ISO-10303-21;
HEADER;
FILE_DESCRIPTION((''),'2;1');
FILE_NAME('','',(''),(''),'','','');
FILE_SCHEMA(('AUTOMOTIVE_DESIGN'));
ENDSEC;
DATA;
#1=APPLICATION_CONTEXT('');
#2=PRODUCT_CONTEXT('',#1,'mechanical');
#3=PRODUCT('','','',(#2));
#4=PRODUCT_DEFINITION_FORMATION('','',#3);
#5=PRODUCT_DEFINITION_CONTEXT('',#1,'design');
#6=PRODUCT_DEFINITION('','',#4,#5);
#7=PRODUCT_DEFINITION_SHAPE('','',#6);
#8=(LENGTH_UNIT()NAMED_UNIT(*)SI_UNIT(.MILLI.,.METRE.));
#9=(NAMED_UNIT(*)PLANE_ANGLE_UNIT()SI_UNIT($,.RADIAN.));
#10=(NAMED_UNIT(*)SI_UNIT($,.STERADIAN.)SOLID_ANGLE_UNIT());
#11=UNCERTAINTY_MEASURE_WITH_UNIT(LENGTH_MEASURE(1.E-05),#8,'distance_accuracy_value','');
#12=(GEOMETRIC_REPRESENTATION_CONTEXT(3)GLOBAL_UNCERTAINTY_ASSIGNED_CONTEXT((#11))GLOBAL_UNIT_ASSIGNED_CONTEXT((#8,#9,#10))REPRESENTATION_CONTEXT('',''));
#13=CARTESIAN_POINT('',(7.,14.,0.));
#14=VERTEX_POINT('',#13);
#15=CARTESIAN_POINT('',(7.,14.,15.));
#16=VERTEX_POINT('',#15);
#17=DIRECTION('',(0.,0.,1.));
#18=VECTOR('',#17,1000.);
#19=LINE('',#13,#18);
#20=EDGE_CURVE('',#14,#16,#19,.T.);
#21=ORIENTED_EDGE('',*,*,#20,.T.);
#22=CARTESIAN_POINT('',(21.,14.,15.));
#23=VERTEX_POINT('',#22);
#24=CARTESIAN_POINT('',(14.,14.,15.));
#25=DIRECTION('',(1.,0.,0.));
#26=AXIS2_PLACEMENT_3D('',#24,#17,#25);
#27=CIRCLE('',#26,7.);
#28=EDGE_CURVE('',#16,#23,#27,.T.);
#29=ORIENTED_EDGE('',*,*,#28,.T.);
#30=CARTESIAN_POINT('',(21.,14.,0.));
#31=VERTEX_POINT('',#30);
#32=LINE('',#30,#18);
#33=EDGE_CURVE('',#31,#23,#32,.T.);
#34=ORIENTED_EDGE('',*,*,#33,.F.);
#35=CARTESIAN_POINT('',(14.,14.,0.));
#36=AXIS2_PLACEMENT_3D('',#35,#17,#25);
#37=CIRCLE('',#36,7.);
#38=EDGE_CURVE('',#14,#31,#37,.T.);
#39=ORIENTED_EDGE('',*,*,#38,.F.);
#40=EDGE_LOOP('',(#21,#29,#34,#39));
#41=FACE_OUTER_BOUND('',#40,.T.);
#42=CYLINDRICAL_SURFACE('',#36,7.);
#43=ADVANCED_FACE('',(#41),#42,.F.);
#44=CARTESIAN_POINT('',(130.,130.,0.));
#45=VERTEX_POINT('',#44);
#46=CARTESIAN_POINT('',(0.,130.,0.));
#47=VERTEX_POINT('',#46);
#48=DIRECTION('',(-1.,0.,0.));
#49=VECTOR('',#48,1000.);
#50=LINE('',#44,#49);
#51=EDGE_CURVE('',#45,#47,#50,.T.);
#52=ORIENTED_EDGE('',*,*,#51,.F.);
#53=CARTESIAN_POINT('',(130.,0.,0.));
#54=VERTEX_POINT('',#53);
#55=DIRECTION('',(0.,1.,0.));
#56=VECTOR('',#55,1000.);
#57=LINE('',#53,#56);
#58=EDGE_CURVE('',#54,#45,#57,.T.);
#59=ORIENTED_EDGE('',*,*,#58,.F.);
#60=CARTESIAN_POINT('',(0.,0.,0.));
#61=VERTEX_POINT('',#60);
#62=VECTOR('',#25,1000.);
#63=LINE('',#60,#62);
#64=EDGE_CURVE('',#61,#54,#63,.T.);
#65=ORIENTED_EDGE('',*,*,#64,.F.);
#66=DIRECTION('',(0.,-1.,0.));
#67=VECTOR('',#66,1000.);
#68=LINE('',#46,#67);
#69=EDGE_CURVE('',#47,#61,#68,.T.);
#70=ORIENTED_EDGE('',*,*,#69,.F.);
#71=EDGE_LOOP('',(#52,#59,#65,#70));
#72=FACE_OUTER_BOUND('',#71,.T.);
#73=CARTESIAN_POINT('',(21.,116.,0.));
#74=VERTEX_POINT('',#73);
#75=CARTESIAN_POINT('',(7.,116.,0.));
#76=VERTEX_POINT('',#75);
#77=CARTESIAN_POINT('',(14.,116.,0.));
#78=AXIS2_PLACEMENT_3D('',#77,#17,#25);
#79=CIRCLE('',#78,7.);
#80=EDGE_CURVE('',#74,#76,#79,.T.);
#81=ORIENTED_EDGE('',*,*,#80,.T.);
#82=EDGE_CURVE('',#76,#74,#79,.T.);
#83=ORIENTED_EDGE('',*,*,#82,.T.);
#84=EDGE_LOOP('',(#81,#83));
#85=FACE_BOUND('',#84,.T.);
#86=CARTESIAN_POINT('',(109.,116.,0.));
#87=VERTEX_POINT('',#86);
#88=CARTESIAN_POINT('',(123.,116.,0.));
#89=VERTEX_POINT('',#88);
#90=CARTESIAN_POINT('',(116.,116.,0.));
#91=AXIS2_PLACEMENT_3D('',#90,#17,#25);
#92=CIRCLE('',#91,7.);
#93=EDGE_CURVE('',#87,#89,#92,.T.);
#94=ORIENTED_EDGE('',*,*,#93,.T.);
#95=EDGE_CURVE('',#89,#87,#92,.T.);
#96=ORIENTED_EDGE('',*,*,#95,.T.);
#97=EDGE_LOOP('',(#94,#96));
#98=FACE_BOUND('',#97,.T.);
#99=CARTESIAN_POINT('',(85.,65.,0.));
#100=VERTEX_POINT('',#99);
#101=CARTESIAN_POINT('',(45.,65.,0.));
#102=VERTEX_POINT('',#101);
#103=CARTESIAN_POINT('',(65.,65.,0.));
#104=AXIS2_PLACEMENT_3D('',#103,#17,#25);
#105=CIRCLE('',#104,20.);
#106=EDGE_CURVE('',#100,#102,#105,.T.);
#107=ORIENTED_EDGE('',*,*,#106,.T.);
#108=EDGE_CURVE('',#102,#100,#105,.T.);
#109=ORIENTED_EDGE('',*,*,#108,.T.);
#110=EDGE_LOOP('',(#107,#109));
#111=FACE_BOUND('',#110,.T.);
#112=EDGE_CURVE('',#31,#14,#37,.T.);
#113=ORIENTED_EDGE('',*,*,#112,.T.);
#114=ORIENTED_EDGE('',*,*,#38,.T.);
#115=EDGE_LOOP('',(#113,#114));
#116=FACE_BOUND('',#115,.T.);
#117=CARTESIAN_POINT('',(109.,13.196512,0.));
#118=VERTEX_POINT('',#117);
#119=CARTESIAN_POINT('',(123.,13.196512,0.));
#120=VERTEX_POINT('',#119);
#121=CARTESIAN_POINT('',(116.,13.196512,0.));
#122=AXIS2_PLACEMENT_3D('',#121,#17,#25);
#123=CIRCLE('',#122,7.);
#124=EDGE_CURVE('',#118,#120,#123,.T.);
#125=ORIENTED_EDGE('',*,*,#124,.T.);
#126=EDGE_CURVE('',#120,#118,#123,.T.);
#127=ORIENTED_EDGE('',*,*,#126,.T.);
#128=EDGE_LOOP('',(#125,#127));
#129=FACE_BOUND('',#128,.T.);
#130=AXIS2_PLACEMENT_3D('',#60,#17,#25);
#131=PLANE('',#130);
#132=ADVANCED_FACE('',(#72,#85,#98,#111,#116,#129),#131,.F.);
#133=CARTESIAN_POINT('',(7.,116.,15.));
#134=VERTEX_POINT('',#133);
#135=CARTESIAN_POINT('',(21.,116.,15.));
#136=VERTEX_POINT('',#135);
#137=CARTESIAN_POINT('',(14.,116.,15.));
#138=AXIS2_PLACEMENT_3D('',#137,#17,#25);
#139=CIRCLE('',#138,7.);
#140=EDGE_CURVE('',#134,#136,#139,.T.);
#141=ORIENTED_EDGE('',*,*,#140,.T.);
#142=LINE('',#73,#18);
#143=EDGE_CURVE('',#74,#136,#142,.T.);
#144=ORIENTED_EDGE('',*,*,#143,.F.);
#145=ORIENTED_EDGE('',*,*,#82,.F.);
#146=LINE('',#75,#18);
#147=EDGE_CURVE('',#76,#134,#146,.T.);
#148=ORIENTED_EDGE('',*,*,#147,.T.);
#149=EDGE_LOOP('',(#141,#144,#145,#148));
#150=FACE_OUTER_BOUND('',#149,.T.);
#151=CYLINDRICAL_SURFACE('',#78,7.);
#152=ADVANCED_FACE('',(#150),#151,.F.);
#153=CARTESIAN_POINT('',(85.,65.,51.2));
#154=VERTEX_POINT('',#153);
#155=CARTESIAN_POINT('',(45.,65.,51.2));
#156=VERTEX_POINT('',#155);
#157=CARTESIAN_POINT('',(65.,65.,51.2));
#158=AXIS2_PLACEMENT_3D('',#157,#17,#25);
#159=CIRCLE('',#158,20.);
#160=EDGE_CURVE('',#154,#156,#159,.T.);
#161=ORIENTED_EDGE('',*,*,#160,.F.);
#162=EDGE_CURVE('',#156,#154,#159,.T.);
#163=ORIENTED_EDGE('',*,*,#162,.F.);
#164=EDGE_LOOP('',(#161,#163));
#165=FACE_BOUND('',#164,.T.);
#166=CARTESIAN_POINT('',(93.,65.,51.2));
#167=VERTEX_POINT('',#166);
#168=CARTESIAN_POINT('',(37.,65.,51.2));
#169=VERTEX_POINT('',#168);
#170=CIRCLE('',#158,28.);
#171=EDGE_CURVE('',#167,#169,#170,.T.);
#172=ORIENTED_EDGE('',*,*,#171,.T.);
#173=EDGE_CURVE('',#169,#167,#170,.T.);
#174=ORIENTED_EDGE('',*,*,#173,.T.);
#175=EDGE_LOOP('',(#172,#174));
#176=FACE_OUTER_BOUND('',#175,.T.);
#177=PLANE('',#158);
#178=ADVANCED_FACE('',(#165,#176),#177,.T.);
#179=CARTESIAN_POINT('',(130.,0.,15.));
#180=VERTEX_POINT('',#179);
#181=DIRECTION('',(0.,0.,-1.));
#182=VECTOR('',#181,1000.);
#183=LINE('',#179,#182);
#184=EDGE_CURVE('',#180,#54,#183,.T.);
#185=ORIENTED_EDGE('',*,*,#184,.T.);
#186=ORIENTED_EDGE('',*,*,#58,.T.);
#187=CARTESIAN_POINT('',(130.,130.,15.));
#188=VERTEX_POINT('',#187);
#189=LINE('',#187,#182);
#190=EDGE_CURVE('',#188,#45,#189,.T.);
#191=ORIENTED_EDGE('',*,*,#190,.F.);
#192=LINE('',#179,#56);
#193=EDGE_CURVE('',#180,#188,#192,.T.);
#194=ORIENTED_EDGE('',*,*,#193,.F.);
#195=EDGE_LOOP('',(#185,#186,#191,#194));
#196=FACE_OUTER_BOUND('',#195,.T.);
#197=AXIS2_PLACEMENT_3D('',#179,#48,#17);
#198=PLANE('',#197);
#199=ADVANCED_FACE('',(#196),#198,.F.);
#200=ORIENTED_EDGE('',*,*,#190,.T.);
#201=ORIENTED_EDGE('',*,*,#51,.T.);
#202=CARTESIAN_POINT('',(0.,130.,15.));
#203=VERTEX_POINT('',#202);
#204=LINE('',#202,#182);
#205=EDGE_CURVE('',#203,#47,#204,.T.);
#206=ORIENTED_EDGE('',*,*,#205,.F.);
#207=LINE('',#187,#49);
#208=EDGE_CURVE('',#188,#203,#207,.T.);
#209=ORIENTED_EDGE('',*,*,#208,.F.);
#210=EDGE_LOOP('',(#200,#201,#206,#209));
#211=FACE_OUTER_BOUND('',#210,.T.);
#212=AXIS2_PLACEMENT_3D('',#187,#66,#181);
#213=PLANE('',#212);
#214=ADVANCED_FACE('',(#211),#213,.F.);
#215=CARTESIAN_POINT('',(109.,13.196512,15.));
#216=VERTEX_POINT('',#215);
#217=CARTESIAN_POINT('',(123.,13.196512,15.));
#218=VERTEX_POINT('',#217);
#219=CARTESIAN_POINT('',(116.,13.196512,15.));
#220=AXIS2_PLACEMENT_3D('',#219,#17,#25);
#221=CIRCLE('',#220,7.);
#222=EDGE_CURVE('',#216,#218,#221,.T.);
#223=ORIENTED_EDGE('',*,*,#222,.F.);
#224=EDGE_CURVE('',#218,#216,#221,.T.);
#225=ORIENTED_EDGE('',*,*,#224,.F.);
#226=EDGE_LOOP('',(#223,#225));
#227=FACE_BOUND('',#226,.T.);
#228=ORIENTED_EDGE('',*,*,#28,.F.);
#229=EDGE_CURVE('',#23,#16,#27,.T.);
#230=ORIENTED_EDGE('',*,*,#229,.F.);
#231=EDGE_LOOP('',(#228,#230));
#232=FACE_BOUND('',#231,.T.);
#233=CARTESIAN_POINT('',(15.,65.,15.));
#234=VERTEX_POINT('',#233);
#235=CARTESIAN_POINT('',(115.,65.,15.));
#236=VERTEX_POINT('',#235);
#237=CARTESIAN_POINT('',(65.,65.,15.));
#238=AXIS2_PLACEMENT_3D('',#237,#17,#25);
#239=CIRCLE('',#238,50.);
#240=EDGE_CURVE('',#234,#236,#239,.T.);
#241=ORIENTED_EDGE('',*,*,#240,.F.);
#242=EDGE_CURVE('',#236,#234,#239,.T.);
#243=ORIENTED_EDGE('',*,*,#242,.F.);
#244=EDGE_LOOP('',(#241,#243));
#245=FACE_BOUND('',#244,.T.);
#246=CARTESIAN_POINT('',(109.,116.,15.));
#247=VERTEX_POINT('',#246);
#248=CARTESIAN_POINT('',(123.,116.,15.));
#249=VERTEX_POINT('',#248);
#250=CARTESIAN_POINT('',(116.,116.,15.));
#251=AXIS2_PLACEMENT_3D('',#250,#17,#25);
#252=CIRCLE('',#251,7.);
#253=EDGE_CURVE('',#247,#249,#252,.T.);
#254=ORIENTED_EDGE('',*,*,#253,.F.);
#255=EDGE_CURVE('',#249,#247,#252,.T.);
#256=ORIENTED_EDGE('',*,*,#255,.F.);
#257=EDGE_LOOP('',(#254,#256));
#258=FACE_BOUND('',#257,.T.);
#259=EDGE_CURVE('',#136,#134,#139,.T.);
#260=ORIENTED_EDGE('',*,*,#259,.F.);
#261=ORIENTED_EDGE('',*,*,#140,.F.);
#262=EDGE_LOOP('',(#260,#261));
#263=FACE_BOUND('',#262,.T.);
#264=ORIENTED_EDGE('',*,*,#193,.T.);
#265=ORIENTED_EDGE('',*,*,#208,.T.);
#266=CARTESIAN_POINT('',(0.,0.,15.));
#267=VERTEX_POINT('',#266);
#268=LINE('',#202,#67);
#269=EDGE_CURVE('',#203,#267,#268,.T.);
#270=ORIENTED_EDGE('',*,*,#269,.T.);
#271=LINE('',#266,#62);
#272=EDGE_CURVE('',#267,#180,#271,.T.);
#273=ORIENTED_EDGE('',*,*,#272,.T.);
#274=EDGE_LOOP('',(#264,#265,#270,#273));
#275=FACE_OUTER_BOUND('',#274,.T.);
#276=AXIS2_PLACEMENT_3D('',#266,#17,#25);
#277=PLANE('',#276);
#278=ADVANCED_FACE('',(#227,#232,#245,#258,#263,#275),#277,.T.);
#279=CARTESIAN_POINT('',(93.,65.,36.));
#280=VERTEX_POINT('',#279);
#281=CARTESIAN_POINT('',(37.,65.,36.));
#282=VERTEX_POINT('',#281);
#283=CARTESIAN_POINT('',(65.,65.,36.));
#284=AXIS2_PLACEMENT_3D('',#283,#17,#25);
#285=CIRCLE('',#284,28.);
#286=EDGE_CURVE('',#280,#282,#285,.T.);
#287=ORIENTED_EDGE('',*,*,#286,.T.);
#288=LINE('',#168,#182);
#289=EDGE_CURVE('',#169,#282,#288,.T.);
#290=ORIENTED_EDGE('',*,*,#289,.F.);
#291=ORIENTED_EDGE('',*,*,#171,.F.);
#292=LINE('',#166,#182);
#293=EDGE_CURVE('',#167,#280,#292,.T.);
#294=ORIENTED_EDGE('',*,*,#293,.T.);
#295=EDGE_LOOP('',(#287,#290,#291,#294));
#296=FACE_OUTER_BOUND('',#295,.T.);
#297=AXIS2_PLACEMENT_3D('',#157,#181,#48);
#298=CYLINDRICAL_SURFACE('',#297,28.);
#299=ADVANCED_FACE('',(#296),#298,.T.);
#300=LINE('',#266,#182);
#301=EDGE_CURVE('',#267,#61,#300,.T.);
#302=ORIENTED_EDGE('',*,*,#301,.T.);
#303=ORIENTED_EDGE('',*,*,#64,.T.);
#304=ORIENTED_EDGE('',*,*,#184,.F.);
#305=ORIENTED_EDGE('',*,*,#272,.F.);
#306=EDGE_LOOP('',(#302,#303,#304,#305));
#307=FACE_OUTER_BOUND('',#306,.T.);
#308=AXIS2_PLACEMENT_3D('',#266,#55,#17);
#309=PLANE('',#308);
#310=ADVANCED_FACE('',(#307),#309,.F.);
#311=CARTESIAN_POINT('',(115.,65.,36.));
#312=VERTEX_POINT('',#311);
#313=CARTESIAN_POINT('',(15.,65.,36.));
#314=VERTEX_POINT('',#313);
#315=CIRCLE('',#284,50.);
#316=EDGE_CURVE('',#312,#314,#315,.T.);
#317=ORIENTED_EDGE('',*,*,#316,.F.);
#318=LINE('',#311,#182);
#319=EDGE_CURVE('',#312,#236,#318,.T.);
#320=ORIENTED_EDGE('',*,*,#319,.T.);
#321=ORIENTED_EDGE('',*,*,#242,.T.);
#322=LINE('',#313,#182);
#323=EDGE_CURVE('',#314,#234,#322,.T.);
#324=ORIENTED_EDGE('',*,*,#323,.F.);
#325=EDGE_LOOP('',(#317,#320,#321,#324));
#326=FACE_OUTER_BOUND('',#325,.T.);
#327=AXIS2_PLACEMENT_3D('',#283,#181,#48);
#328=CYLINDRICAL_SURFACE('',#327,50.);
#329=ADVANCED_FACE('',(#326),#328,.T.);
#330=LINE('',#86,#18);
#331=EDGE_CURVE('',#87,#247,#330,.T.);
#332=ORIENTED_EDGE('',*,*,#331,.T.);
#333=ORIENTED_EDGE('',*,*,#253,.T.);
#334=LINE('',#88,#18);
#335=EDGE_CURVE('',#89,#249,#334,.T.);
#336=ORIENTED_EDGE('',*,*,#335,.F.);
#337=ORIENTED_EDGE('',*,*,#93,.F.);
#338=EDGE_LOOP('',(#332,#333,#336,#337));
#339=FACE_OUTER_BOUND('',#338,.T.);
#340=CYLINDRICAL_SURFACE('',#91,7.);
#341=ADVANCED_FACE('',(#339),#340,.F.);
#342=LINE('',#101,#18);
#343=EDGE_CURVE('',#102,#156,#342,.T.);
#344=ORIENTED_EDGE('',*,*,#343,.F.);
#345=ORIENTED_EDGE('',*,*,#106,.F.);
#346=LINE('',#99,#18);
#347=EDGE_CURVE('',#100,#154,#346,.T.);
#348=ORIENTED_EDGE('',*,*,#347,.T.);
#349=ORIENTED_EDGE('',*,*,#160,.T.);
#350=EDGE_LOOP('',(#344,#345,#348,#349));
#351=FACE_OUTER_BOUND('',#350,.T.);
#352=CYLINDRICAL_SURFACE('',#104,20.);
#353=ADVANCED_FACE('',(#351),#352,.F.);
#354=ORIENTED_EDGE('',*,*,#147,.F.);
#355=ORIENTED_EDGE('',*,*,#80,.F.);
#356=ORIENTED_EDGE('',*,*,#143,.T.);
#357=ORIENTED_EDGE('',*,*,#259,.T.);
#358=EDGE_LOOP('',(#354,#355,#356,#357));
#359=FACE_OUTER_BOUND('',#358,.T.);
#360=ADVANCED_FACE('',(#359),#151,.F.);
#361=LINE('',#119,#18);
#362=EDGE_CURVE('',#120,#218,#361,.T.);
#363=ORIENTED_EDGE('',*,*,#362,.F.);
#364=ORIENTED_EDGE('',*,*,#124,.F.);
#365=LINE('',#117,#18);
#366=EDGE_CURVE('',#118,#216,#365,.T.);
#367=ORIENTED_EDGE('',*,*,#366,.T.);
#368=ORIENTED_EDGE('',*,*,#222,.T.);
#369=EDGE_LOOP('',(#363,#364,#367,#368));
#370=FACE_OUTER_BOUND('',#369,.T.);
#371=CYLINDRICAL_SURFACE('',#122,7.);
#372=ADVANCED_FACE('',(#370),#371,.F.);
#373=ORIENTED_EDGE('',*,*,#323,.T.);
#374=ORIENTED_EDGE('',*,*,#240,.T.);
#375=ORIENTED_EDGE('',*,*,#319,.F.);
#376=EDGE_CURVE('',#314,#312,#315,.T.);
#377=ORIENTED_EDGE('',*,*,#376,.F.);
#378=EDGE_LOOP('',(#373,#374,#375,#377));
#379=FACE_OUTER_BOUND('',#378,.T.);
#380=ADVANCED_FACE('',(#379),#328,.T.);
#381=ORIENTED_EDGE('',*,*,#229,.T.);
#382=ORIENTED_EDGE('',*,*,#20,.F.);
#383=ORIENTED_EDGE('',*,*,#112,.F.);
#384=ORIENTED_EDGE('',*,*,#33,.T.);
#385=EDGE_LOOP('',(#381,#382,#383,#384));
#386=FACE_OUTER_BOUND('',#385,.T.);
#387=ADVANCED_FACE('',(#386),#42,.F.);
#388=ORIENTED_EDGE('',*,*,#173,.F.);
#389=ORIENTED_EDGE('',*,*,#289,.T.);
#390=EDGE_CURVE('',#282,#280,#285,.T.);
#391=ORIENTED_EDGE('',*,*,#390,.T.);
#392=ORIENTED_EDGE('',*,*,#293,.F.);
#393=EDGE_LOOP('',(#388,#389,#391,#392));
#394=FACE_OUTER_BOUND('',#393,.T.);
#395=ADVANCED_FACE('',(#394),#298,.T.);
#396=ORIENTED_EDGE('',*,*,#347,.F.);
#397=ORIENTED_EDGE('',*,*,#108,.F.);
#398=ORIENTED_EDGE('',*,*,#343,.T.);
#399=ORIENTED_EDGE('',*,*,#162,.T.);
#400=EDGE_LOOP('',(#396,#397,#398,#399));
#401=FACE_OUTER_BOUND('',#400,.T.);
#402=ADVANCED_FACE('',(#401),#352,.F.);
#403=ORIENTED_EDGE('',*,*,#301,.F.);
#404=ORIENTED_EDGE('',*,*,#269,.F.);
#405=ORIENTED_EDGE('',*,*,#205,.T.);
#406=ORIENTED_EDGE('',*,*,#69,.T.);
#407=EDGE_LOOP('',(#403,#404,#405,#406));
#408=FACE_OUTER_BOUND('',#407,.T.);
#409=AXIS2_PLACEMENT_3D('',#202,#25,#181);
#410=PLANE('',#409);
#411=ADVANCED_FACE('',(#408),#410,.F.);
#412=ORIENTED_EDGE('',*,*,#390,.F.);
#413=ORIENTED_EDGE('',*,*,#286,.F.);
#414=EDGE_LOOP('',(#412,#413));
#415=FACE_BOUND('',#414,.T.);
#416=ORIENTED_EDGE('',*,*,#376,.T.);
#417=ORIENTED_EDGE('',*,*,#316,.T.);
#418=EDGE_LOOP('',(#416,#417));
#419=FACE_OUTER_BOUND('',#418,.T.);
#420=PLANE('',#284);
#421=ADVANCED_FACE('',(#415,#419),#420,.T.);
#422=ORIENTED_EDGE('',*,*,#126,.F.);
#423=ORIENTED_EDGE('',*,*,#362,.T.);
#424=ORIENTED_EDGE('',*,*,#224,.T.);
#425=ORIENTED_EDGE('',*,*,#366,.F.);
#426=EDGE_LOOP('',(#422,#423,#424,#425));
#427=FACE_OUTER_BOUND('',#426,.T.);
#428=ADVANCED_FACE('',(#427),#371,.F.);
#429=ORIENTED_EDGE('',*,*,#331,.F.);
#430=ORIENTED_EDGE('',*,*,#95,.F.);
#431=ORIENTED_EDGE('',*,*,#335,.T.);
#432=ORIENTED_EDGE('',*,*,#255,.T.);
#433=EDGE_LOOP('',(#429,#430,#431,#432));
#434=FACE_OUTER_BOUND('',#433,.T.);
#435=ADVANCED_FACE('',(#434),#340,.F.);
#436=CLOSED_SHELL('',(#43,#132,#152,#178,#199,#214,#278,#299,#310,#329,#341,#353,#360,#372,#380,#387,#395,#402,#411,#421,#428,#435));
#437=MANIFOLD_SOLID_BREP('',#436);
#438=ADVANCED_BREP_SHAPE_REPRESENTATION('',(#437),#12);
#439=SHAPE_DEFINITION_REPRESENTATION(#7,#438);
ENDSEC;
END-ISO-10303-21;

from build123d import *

# Parameters (mm, degrees)
FLANGE_PLATE_SKETCH_W         = 130
FLANGE_PLATE_SKETCH_H         = 130
FLANGE_PLATE_130X130X15_DEPTH = 15
HUB_SKETCH_100_R              = 50
HUB_100_DEPTH                 = 21
SPIGOT_SKETCH_56_R            = 28
SPIGOT_56_DEPTH               = 15.2
BORE_SKETCH_40_R              = 20
BORE_40_DEPTH                 = 51.2
MOUNTING_HOLES_SKETCH_R       = 7
MOUNTING_HOLES_4X_14_DEPTH    = 15


with BuildPart() as part:
    # Flange Plate Sketch → Flange Plate 130x130x15 (new body)
    with BuildSketch(Plane.XY):
        with Locations((65, 65)):
            Rectangle(FLANGE_PLATE_SKETCH_W, FLANGE_PLATE_SKETCH_H)
    extrude(amount=FLANGE_PLATE_130X130X15_DEPTH)

    # Hub Sketch Ø100 → Hub Ø100 (add)
    with BuildSketch(Plane.XY.offset(15)):
        with Locations(Location((65, 65, 0), (0, 0, 180))):
            Circle(HUB_SKETCH_100_R)
    extrude(amount=HUB_100_DEPTH)

    # Spigot Sketch Ø56 → Spigot Ø56 (add)
    with BuildSketch(Plane.XY.offset(36)):
        with Locations(Location((65, 65, 0), (0, 0, 180))):
            Circle(SPIGOT_SKETCH_56_R)
    extrude(amount=SPIGOT_56_DEPTH)

    # Bore Sketch Ø40 → Bore Ø40 (cut)
    with BuildSketch(Plane.XY.offset(51.2)):
        with Locations((65, 65)):
            Circle(BORE_SKETCH_40_R)
    extrude(amount=-BORE_40_DEPTH, mode=Mode.SUBTRACT)

    # Mounting Holes Sketch → Mounting Holes 4xØ14 (cut)
    with BuildSketch(Plane.XY.offset(15)):
        with Locations((116, 116)):
            Circle(MOUNTING_HOLES_SKETCH_R)
        with Locations((14, 116)):
            Circle(MOUNTING_HOLES_SKETCH_R)
        with Locations((14, 14)):
            Circle(MOUNTING_HOLES_SKETCH_R)
        with Locations((116, 13.196511798)):
            Circle(MOUNTING_HOLES_SKETCH_R)
    extrude(amount=-MOUNTING_HOLES_4X_14_DEPTH, mode=Mode.SUBTRACT)


solid = part.part
